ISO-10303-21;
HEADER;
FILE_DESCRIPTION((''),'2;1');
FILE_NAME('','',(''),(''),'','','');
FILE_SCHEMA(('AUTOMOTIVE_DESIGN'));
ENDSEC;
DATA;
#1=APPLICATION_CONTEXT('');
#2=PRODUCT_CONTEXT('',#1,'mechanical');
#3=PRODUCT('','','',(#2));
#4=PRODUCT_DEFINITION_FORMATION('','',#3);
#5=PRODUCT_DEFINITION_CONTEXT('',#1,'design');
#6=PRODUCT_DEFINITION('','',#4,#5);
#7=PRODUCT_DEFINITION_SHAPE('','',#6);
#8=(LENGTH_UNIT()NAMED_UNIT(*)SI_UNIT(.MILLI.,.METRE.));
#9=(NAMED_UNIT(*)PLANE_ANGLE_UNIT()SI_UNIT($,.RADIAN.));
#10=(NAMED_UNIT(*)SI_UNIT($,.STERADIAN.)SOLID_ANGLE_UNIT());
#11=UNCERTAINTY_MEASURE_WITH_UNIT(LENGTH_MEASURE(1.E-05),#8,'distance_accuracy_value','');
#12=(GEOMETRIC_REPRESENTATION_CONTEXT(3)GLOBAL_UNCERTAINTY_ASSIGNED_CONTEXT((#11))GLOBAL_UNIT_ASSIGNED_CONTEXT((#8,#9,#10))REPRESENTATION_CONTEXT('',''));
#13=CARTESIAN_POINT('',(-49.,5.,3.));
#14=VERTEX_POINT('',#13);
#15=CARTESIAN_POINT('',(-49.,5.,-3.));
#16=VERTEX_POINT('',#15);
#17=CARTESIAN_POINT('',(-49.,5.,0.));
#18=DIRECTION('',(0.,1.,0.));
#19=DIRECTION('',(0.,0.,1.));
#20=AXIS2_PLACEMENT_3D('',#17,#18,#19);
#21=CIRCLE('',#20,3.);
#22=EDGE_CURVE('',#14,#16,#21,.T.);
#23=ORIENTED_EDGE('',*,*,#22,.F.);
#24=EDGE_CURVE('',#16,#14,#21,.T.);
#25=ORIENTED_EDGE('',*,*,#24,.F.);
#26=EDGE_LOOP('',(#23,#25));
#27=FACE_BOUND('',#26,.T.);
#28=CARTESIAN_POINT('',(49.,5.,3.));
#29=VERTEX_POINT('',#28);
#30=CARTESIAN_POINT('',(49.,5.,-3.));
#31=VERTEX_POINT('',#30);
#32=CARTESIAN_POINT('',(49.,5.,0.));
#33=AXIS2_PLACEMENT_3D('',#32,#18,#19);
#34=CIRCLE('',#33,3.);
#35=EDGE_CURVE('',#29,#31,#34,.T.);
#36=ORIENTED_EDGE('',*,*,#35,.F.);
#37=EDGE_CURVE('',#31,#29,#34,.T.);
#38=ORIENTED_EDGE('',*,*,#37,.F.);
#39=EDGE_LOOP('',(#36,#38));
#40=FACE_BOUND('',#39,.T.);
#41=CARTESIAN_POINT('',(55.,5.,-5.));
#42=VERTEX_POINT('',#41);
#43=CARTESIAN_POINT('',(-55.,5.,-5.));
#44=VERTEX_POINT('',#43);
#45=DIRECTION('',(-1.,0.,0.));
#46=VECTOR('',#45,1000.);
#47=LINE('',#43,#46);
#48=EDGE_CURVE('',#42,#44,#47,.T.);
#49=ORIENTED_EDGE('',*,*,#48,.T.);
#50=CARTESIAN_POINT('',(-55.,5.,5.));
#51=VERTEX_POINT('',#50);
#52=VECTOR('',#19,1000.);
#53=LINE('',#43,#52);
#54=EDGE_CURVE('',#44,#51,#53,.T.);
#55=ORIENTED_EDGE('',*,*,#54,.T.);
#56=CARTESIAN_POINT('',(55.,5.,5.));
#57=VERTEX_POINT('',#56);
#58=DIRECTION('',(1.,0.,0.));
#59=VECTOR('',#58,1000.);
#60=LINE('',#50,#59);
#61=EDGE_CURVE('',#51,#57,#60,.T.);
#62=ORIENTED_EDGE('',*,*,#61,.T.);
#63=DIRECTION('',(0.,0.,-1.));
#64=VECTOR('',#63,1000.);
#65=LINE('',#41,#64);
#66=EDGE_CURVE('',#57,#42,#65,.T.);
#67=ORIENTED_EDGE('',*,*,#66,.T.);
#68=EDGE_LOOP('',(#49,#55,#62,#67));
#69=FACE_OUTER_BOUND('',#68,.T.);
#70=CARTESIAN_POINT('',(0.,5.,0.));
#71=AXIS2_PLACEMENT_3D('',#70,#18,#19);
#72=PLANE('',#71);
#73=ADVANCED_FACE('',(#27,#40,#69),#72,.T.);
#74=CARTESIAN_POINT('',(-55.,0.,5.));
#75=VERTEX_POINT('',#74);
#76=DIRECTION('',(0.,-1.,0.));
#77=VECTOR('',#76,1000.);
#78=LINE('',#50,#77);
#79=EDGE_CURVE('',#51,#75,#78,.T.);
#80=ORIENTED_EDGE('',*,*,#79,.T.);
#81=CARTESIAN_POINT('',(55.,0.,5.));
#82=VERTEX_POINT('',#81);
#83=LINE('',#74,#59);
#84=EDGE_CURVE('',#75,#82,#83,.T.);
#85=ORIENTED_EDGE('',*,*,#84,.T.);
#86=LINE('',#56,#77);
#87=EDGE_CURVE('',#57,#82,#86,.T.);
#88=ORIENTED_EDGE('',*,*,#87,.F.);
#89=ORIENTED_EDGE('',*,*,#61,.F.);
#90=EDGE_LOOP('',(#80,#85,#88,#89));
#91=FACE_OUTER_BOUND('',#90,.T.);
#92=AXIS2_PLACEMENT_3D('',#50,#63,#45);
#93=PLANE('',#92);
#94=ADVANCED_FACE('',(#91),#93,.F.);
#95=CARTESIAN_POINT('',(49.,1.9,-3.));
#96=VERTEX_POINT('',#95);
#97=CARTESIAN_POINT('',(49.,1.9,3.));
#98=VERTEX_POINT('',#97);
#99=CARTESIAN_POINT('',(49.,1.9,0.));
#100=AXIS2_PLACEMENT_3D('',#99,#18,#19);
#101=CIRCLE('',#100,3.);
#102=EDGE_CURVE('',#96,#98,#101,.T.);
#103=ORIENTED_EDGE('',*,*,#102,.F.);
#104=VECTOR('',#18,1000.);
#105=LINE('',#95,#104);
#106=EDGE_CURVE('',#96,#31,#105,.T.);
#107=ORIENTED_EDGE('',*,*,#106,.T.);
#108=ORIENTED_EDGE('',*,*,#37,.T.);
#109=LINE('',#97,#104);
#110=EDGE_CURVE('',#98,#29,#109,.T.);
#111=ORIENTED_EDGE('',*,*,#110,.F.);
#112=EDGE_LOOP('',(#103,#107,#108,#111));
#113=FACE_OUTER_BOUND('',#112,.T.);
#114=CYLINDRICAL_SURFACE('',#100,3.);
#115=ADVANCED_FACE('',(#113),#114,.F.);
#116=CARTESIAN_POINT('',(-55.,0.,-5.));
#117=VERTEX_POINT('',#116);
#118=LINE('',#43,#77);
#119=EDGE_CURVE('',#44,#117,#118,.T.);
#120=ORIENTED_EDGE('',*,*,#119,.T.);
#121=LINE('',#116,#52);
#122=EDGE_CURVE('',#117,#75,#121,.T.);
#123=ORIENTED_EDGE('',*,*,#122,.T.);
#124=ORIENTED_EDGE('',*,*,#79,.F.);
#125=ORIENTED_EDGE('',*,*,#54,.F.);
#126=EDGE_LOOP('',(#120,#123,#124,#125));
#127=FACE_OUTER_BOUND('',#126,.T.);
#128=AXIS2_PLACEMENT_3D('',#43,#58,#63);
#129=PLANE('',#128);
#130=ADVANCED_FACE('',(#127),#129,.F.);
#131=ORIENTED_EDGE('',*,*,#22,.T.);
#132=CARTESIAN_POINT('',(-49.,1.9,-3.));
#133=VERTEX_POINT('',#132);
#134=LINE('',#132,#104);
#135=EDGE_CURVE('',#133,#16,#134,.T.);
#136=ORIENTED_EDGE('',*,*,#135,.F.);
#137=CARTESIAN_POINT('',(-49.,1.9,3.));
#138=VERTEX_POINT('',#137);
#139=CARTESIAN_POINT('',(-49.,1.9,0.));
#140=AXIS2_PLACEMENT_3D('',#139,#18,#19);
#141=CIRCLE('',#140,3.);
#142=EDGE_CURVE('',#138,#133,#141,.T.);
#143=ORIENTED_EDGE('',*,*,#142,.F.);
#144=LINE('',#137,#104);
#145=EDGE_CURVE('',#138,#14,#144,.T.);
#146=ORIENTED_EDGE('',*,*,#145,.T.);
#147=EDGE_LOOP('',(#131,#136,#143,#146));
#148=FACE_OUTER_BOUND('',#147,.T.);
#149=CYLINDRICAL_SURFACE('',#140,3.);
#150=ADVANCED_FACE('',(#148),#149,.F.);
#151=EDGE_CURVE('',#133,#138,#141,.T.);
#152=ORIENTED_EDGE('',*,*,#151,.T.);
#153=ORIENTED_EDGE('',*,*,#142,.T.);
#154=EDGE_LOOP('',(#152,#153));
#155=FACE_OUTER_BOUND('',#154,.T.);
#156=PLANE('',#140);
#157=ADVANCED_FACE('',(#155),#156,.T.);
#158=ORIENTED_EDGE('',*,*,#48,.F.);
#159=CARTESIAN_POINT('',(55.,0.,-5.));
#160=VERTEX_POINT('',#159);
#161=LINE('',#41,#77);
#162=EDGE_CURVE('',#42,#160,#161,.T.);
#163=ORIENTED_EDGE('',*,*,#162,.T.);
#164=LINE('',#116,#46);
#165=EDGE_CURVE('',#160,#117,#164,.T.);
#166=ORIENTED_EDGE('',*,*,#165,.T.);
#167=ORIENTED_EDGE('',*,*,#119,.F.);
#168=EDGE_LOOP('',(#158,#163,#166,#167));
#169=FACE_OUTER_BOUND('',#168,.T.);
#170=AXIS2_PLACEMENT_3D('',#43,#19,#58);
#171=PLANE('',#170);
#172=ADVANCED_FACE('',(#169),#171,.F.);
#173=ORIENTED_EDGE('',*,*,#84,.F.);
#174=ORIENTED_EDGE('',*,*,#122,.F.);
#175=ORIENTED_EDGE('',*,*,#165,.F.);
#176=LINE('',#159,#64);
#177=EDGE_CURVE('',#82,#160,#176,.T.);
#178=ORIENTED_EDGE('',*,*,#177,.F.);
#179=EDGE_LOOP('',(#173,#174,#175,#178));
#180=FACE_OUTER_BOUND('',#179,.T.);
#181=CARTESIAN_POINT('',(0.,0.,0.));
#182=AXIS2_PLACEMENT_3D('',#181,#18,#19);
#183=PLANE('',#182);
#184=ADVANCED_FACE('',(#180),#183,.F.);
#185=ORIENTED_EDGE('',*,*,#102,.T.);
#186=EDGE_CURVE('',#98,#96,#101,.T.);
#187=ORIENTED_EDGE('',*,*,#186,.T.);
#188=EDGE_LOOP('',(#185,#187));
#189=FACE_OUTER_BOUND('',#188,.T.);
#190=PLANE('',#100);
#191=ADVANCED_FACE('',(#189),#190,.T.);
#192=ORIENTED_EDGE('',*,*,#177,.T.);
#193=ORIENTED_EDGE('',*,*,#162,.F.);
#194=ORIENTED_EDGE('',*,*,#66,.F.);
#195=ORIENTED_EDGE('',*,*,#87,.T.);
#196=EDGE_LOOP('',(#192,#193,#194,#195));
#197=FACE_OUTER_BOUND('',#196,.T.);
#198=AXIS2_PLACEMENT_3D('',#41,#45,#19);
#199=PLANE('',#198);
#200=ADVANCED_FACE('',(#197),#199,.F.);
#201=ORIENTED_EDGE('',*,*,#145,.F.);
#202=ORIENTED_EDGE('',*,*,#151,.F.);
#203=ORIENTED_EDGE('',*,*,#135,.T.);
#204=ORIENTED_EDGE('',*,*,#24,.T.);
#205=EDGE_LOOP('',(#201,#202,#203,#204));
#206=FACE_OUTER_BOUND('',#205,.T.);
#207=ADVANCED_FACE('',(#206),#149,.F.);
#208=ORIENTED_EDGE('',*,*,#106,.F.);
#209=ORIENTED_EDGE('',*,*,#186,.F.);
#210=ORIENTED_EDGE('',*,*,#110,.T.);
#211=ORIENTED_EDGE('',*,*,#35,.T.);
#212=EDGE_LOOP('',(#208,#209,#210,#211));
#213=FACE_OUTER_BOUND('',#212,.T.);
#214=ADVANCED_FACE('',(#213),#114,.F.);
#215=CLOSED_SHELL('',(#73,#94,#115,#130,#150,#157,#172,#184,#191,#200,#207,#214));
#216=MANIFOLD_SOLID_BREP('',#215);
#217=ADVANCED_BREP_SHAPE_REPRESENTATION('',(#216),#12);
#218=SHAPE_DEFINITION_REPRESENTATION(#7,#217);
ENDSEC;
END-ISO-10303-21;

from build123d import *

# Parameters (mm, degrees)
SKETCH1_W           = 110
SKETCH1_H           = 10
BOSS_EXTRUDE1_DEPTH = 5
SKETCH2_R           = 3
CUT_EXTRUDE1_DEPTH  = 3.1


with BuildPart() as part:
    # Sketch1 → Boss-Extrude1 (new body)
    with BuildSketch(Plane(origin=(0, 0, 0), x_dir=(1, 0, 0), z_dir=(0, 1, 0))):
        Rectangle(SKETCH1_W, SKETCH1_H)
    extrude(amount=BOSS_EXTRUDE1_DEPTH)

    # Sketch2 → Cut-Extrude1 (cut)
    with BuildSketch(Plane(origin=(0, 5, 0), x_dir=(1, 0, 0), z_dir=(0, 1, 0))):
        with Locations(Location((-49, 0, 0), (0, 0, 270))):
            Circle(SKETCH2_R)
        with Locations(Location((49, 0, 0), (0, 0, 270))):
            Circle(SKETCH2_R)
    extrude(amount=-CUT_EXTRUDE1_DEPTH, mode=Mode.SUBTRACT)


solid = part.part
